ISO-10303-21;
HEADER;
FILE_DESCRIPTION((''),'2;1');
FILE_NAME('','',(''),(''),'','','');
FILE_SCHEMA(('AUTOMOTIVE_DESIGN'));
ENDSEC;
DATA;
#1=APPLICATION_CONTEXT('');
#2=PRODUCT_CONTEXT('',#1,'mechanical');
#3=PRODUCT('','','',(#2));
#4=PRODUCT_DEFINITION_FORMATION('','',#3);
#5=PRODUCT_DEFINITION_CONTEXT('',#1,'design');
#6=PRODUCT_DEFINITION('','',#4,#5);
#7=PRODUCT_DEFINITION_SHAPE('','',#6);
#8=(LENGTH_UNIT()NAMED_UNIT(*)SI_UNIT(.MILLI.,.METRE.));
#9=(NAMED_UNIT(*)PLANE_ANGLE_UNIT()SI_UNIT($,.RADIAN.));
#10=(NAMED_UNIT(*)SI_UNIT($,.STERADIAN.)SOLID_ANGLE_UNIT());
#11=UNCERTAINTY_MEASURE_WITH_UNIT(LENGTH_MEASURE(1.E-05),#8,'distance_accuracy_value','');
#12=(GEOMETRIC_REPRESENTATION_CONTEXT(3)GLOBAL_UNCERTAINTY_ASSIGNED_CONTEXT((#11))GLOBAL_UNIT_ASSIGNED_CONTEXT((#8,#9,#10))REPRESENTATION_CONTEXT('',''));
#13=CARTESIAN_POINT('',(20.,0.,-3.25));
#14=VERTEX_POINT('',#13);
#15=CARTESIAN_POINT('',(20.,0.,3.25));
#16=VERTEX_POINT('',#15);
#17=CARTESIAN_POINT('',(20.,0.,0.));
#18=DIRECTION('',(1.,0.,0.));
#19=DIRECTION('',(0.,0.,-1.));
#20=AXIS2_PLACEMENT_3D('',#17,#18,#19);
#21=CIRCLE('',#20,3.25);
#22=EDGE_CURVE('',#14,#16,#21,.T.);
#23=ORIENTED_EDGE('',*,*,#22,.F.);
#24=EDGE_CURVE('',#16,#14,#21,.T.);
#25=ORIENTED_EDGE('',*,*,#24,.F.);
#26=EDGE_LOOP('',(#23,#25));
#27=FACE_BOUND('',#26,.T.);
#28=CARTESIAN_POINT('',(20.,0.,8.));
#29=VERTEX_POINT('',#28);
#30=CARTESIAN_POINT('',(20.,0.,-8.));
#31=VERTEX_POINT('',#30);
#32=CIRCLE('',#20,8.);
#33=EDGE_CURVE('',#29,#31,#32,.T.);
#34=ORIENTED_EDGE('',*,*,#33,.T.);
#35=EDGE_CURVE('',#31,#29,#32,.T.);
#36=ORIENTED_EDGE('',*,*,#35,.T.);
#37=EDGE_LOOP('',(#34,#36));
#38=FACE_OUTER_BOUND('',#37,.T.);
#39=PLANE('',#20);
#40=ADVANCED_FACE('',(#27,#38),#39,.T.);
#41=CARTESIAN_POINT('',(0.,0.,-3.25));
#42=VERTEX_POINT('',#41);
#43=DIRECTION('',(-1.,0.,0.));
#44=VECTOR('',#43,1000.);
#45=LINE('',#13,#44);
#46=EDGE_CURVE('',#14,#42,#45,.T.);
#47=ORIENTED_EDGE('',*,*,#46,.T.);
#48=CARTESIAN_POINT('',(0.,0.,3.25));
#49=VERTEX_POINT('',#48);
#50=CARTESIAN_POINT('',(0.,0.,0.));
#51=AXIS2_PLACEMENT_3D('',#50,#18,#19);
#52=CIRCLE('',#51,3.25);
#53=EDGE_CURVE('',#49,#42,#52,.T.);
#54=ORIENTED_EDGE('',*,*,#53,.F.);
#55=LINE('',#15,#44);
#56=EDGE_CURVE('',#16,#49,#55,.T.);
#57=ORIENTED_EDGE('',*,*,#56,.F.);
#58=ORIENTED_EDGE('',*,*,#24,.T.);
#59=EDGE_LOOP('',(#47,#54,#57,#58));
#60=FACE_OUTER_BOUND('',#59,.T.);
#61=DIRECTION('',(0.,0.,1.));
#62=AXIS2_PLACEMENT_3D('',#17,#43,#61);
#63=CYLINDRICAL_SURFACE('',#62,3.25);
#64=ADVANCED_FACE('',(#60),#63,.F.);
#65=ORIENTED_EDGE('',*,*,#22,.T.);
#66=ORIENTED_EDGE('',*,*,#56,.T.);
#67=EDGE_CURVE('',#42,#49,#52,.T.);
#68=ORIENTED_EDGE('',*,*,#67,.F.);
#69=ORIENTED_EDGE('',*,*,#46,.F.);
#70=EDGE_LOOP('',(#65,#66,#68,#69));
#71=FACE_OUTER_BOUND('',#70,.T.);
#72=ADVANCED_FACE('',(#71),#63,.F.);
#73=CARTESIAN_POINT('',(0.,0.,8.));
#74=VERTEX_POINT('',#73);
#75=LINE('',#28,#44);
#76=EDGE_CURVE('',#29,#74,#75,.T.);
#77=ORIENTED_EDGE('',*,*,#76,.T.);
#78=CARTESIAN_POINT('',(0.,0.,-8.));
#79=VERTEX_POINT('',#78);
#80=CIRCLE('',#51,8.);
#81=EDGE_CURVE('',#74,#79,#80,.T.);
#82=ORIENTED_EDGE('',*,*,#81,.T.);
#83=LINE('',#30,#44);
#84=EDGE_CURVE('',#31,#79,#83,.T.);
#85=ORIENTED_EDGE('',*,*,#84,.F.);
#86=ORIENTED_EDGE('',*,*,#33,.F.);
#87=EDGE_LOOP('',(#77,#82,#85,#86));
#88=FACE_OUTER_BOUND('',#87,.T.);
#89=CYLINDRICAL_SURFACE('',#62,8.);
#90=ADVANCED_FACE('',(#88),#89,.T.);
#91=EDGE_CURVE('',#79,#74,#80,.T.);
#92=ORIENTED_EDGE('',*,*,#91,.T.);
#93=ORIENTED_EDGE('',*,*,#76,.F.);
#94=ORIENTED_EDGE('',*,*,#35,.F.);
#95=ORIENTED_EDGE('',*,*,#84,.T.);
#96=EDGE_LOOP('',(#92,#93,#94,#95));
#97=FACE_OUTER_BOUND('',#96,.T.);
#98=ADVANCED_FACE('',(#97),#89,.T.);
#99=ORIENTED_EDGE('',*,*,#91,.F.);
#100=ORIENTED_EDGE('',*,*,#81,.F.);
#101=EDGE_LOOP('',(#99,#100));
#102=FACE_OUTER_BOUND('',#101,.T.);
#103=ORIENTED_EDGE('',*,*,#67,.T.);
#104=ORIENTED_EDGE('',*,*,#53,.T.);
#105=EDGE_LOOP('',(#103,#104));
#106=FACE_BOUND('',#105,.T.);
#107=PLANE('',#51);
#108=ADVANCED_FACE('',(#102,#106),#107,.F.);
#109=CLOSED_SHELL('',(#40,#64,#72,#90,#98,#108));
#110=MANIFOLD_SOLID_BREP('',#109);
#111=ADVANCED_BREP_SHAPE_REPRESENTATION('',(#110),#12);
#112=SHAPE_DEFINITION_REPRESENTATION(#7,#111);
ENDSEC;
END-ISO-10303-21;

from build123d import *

# Parameters (mm, degrees)
SKETCH_1_R      = 8
SKETCH_1_R_2    = 3.25
EXTRUDE_1_DEPTH = 20


with BuildPart() as part:
    # 草图1 → 凸台-拉伸1 (new body)
    with BuildSketch(Plane(origin=(0, 0, 0), x_dir=(0, 0, -1), z_dir=(1, 0, 0))):
        Circle(SKETCH_1_R)
        Circle(SKETCH_1_R_2, mode=Mode.SUBTRACT)
    extrude(amount=EXTRUDE_1_DEPTH)


solid = part.part
